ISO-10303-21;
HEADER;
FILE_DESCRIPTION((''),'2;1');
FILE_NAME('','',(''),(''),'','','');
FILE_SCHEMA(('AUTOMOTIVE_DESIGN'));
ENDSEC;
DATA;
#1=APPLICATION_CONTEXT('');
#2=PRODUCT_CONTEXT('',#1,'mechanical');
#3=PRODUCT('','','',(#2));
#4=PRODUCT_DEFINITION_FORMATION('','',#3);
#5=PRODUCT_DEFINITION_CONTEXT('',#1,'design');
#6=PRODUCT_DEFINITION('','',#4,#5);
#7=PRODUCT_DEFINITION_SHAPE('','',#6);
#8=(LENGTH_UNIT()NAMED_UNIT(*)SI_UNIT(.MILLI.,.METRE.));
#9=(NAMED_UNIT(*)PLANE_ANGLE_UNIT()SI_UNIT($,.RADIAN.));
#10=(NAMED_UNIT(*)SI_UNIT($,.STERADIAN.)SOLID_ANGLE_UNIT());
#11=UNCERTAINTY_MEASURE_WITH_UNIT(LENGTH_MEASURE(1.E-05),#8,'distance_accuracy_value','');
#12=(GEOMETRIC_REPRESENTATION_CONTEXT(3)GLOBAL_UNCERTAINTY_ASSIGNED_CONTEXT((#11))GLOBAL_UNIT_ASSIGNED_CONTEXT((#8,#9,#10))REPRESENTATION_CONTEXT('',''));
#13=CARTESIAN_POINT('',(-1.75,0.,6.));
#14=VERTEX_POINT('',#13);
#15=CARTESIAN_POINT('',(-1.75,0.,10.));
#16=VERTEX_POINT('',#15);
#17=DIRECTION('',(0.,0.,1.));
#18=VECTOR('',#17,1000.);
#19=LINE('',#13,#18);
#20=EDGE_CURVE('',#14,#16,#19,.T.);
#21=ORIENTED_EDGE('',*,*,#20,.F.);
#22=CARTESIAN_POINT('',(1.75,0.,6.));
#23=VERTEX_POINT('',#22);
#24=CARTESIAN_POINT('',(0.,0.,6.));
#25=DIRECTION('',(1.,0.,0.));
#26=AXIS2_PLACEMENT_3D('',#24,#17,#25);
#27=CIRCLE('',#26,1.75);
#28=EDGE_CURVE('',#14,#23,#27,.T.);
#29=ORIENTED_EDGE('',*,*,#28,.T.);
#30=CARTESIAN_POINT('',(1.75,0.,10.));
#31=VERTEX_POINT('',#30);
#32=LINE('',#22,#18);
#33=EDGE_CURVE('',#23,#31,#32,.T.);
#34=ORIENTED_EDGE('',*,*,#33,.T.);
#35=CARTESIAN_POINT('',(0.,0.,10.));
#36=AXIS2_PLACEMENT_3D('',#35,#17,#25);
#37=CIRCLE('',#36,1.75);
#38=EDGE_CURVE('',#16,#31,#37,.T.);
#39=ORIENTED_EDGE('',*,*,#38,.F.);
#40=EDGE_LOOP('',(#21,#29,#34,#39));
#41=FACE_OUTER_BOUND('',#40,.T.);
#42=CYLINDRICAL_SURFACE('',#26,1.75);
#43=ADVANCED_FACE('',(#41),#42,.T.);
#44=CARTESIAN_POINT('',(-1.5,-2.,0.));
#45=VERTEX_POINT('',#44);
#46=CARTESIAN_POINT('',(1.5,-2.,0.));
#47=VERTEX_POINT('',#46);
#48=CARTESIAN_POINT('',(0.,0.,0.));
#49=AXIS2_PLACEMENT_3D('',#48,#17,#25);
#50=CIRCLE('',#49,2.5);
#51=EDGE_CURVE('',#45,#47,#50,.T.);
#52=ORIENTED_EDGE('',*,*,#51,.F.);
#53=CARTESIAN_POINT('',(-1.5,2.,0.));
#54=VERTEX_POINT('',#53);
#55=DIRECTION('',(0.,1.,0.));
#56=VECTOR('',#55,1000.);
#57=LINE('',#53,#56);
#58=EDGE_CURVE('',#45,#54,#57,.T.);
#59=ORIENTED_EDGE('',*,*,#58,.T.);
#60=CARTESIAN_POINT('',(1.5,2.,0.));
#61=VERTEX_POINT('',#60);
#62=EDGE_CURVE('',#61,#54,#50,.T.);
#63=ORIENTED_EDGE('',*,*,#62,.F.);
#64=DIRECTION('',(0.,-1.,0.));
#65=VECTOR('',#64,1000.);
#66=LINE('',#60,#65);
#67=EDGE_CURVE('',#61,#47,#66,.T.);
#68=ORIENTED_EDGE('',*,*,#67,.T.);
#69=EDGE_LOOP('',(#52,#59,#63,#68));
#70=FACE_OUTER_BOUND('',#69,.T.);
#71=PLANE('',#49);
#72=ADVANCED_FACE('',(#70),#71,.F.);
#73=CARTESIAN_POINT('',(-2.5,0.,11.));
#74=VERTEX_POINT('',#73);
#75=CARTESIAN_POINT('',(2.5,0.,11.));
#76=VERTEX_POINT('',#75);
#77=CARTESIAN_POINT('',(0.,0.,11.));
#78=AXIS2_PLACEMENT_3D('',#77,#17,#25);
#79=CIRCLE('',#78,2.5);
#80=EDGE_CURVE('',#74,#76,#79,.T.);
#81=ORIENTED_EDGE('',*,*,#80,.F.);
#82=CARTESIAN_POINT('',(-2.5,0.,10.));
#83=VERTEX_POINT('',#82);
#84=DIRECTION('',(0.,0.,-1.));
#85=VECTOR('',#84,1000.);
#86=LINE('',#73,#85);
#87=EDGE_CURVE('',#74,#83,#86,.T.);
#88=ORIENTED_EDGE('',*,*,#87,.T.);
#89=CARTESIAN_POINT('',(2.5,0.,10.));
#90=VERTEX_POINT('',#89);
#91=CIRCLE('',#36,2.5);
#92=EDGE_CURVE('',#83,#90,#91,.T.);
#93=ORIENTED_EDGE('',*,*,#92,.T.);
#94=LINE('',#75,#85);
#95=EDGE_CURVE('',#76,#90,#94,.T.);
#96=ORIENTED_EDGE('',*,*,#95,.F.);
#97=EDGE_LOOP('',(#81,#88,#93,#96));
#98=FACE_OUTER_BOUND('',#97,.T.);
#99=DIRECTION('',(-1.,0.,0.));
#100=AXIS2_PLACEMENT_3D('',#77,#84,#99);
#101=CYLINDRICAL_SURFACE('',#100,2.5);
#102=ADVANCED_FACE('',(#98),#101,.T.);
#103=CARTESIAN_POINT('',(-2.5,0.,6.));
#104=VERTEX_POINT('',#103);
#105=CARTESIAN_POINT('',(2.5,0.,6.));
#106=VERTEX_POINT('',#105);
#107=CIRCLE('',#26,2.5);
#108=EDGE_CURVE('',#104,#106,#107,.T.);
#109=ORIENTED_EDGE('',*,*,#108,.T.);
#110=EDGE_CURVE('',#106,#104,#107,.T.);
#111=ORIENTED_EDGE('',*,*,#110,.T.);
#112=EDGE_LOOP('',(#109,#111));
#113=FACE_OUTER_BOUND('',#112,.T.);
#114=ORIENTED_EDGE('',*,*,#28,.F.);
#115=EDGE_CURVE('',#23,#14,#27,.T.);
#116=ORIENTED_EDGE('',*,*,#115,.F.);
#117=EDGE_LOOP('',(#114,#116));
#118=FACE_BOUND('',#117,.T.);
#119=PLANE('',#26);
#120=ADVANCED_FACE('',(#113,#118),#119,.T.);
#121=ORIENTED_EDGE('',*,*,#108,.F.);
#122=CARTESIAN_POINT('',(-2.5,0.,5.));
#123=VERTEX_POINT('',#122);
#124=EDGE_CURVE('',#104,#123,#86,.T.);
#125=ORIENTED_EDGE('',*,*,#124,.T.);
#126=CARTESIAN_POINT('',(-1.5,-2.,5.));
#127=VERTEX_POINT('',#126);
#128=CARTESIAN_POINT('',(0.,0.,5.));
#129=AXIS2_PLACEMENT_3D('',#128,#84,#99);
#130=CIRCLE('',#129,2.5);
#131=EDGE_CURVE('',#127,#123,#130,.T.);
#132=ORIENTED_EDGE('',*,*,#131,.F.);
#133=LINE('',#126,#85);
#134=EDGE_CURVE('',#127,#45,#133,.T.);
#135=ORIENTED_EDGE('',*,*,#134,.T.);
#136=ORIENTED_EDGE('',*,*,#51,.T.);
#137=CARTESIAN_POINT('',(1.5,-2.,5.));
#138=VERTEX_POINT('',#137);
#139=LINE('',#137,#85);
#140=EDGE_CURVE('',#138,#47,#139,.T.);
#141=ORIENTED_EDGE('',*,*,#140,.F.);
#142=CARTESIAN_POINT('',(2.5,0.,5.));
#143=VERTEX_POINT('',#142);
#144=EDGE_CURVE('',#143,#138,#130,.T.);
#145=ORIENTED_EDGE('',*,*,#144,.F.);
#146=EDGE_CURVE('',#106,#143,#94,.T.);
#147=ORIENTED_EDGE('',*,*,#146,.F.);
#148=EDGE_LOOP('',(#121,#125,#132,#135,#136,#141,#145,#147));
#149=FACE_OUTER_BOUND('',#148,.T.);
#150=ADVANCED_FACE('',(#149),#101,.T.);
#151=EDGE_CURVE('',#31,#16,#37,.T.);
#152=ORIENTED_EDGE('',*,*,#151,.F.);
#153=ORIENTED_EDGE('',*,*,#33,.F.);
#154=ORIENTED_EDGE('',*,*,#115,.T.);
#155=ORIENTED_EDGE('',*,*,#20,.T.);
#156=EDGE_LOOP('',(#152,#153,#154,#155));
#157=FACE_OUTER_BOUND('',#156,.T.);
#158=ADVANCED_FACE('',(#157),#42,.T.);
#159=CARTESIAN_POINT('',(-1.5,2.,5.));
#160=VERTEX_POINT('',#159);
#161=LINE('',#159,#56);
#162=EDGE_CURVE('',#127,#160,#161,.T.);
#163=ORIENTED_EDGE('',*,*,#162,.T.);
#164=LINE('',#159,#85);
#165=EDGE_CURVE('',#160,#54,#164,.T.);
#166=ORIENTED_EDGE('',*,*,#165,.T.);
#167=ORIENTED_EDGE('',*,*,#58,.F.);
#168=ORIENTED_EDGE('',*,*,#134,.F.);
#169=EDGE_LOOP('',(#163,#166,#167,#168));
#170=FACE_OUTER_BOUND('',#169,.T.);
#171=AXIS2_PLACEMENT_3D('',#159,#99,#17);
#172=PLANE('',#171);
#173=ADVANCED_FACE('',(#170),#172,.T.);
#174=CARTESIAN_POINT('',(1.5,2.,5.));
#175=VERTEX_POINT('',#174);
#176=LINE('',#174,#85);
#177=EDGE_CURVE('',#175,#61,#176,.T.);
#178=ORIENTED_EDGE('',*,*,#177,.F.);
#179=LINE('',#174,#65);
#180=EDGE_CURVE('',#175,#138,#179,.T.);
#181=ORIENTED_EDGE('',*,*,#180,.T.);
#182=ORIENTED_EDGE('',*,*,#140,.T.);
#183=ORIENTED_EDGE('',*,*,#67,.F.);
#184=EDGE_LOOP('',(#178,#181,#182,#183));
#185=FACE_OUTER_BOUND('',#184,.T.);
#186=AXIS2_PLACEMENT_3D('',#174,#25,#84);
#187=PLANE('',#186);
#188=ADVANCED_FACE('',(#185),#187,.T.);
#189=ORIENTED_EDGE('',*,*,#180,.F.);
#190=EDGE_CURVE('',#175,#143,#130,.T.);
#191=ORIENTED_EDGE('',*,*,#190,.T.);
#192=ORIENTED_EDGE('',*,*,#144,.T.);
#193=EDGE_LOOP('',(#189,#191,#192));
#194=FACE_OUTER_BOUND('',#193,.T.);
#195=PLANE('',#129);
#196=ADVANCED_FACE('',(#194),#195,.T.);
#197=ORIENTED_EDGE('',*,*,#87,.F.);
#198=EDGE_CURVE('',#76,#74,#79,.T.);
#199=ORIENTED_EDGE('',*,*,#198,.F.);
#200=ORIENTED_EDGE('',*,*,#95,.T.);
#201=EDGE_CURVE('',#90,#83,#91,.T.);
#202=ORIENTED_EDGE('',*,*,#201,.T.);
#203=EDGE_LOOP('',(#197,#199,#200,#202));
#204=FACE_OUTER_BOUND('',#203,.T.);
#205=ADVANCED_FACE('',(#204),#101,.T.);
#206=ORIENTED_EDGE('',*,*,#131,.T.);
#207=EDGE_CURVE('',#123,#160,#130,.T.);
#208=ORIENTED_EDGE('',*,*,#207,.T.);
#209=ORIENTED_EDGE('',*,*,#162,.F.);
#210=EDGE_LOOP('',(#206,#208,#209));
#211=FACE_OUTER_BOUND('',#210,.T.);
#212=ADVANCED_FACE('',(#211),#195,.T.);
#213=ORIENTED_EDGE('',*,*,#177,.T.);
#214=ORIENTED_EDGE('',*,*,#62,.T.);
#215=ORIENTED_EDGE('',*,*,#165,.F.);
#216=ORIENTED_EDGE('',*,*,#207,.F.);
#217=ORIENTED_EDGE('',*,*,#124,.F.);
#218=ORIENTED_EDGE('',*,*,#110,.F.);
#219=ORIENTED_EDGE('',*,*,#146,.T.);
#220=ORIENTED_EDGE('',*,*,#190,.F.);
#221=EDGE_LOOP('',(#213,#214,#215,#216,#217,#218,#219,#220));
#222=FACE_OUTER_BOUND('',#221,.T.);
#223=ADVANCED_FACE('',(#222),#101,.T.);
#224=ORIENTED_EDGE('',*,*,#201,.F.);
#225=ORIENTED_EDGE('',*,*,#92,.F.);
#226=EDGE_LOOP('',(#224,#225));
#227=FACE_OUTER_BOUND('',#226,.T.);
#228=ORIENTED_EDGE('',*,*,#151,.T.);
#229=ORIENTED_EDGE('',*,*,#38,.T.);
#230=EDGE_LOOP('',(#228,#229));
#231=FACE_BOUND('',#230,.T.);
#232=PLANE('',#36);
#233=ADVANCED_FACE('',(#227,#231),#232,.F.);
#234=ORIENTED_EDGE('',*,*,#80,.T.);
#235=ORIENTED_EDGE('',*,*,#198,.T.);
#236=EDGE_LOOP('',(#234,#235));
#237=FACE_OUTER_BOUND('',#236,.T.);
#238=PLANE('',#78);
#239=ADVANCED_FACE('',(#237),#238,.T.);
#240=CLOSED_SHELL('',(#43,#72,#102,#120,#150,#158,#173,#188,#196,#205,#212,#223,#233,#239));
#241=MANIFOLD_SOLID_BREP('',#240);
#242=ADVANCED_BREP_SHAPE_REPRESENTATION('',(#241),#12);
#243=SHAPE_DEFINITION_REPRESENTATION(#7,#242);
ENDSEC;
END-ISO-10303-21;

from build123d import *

# Parameters (mm, degrees)
SKETCH1_R           = 2.5
BOSS_EXTRUDE1_DEPTH = 11
SKETCH2_OUTSIDE_W   = 9.616
SKETCH2_OUTSIDE_H   = 9.616
CUT_EXTRUDE1_DEPTH  = 5
CUT_EXTRUDE2_START  = -5
SKETCH3_R           = 2.5
SKETCH3_R_2         = 1.75
CUT_EXTRUDE2_DEPTH  = 4


with BuildPart() as part:
    # Sketch1 → Boss-Extrude1 (new body)
    with BuildSketch(Plane.XY):
        Circle(SKETCH1_R)
    extrude(amount=BOSS_EXTRUDE1_DEPTH)

    # Sketch2 outside → Cut-Extrude1 (cut)
    with BuildSketch(Plane(origin=(0, 0, 0), x_dir=(-1, 0, 0), z_dir=(0, 0, -1))):
        Rectangle(SKETCH2_OUTSIDE_W, SKETCH2_OUTSIDE_H)
        with BuildLine():
            Line((-1.5, 2), (-1.5, -2))
            ThreePointArc((-1.5, -2), (0, -2.5), (1.5, -2))
            Line((1.5, -2), (1.5, 2))
            ThreePointArc((1.5, 2), (0, 2.5), (-1.5, 2))
        make_face(mode=Mode.SUBTRACT)
    extrude(amount=-CUT_EXTRUDE1_DEPTH, mode=Mode.SUBTRACT)

    # Sketch3 → Cut-Extrude2 (cut)
    with BuildSketch(Plane.XY.offset(11).offset(CUT_EXTRUDE2_START)):
        with Locations(Location((0, 0, 0), (0, 0, 126.869897646))):
            Circle(SKETCH3_R)
        Circle(SKETCH3_R_2, mode=Mode.SUBTRACT)
    extrude(amount=CUT_EXTRUDE2_DEPTH, mode=Mode.SUBTRACT)


solid = part.part
